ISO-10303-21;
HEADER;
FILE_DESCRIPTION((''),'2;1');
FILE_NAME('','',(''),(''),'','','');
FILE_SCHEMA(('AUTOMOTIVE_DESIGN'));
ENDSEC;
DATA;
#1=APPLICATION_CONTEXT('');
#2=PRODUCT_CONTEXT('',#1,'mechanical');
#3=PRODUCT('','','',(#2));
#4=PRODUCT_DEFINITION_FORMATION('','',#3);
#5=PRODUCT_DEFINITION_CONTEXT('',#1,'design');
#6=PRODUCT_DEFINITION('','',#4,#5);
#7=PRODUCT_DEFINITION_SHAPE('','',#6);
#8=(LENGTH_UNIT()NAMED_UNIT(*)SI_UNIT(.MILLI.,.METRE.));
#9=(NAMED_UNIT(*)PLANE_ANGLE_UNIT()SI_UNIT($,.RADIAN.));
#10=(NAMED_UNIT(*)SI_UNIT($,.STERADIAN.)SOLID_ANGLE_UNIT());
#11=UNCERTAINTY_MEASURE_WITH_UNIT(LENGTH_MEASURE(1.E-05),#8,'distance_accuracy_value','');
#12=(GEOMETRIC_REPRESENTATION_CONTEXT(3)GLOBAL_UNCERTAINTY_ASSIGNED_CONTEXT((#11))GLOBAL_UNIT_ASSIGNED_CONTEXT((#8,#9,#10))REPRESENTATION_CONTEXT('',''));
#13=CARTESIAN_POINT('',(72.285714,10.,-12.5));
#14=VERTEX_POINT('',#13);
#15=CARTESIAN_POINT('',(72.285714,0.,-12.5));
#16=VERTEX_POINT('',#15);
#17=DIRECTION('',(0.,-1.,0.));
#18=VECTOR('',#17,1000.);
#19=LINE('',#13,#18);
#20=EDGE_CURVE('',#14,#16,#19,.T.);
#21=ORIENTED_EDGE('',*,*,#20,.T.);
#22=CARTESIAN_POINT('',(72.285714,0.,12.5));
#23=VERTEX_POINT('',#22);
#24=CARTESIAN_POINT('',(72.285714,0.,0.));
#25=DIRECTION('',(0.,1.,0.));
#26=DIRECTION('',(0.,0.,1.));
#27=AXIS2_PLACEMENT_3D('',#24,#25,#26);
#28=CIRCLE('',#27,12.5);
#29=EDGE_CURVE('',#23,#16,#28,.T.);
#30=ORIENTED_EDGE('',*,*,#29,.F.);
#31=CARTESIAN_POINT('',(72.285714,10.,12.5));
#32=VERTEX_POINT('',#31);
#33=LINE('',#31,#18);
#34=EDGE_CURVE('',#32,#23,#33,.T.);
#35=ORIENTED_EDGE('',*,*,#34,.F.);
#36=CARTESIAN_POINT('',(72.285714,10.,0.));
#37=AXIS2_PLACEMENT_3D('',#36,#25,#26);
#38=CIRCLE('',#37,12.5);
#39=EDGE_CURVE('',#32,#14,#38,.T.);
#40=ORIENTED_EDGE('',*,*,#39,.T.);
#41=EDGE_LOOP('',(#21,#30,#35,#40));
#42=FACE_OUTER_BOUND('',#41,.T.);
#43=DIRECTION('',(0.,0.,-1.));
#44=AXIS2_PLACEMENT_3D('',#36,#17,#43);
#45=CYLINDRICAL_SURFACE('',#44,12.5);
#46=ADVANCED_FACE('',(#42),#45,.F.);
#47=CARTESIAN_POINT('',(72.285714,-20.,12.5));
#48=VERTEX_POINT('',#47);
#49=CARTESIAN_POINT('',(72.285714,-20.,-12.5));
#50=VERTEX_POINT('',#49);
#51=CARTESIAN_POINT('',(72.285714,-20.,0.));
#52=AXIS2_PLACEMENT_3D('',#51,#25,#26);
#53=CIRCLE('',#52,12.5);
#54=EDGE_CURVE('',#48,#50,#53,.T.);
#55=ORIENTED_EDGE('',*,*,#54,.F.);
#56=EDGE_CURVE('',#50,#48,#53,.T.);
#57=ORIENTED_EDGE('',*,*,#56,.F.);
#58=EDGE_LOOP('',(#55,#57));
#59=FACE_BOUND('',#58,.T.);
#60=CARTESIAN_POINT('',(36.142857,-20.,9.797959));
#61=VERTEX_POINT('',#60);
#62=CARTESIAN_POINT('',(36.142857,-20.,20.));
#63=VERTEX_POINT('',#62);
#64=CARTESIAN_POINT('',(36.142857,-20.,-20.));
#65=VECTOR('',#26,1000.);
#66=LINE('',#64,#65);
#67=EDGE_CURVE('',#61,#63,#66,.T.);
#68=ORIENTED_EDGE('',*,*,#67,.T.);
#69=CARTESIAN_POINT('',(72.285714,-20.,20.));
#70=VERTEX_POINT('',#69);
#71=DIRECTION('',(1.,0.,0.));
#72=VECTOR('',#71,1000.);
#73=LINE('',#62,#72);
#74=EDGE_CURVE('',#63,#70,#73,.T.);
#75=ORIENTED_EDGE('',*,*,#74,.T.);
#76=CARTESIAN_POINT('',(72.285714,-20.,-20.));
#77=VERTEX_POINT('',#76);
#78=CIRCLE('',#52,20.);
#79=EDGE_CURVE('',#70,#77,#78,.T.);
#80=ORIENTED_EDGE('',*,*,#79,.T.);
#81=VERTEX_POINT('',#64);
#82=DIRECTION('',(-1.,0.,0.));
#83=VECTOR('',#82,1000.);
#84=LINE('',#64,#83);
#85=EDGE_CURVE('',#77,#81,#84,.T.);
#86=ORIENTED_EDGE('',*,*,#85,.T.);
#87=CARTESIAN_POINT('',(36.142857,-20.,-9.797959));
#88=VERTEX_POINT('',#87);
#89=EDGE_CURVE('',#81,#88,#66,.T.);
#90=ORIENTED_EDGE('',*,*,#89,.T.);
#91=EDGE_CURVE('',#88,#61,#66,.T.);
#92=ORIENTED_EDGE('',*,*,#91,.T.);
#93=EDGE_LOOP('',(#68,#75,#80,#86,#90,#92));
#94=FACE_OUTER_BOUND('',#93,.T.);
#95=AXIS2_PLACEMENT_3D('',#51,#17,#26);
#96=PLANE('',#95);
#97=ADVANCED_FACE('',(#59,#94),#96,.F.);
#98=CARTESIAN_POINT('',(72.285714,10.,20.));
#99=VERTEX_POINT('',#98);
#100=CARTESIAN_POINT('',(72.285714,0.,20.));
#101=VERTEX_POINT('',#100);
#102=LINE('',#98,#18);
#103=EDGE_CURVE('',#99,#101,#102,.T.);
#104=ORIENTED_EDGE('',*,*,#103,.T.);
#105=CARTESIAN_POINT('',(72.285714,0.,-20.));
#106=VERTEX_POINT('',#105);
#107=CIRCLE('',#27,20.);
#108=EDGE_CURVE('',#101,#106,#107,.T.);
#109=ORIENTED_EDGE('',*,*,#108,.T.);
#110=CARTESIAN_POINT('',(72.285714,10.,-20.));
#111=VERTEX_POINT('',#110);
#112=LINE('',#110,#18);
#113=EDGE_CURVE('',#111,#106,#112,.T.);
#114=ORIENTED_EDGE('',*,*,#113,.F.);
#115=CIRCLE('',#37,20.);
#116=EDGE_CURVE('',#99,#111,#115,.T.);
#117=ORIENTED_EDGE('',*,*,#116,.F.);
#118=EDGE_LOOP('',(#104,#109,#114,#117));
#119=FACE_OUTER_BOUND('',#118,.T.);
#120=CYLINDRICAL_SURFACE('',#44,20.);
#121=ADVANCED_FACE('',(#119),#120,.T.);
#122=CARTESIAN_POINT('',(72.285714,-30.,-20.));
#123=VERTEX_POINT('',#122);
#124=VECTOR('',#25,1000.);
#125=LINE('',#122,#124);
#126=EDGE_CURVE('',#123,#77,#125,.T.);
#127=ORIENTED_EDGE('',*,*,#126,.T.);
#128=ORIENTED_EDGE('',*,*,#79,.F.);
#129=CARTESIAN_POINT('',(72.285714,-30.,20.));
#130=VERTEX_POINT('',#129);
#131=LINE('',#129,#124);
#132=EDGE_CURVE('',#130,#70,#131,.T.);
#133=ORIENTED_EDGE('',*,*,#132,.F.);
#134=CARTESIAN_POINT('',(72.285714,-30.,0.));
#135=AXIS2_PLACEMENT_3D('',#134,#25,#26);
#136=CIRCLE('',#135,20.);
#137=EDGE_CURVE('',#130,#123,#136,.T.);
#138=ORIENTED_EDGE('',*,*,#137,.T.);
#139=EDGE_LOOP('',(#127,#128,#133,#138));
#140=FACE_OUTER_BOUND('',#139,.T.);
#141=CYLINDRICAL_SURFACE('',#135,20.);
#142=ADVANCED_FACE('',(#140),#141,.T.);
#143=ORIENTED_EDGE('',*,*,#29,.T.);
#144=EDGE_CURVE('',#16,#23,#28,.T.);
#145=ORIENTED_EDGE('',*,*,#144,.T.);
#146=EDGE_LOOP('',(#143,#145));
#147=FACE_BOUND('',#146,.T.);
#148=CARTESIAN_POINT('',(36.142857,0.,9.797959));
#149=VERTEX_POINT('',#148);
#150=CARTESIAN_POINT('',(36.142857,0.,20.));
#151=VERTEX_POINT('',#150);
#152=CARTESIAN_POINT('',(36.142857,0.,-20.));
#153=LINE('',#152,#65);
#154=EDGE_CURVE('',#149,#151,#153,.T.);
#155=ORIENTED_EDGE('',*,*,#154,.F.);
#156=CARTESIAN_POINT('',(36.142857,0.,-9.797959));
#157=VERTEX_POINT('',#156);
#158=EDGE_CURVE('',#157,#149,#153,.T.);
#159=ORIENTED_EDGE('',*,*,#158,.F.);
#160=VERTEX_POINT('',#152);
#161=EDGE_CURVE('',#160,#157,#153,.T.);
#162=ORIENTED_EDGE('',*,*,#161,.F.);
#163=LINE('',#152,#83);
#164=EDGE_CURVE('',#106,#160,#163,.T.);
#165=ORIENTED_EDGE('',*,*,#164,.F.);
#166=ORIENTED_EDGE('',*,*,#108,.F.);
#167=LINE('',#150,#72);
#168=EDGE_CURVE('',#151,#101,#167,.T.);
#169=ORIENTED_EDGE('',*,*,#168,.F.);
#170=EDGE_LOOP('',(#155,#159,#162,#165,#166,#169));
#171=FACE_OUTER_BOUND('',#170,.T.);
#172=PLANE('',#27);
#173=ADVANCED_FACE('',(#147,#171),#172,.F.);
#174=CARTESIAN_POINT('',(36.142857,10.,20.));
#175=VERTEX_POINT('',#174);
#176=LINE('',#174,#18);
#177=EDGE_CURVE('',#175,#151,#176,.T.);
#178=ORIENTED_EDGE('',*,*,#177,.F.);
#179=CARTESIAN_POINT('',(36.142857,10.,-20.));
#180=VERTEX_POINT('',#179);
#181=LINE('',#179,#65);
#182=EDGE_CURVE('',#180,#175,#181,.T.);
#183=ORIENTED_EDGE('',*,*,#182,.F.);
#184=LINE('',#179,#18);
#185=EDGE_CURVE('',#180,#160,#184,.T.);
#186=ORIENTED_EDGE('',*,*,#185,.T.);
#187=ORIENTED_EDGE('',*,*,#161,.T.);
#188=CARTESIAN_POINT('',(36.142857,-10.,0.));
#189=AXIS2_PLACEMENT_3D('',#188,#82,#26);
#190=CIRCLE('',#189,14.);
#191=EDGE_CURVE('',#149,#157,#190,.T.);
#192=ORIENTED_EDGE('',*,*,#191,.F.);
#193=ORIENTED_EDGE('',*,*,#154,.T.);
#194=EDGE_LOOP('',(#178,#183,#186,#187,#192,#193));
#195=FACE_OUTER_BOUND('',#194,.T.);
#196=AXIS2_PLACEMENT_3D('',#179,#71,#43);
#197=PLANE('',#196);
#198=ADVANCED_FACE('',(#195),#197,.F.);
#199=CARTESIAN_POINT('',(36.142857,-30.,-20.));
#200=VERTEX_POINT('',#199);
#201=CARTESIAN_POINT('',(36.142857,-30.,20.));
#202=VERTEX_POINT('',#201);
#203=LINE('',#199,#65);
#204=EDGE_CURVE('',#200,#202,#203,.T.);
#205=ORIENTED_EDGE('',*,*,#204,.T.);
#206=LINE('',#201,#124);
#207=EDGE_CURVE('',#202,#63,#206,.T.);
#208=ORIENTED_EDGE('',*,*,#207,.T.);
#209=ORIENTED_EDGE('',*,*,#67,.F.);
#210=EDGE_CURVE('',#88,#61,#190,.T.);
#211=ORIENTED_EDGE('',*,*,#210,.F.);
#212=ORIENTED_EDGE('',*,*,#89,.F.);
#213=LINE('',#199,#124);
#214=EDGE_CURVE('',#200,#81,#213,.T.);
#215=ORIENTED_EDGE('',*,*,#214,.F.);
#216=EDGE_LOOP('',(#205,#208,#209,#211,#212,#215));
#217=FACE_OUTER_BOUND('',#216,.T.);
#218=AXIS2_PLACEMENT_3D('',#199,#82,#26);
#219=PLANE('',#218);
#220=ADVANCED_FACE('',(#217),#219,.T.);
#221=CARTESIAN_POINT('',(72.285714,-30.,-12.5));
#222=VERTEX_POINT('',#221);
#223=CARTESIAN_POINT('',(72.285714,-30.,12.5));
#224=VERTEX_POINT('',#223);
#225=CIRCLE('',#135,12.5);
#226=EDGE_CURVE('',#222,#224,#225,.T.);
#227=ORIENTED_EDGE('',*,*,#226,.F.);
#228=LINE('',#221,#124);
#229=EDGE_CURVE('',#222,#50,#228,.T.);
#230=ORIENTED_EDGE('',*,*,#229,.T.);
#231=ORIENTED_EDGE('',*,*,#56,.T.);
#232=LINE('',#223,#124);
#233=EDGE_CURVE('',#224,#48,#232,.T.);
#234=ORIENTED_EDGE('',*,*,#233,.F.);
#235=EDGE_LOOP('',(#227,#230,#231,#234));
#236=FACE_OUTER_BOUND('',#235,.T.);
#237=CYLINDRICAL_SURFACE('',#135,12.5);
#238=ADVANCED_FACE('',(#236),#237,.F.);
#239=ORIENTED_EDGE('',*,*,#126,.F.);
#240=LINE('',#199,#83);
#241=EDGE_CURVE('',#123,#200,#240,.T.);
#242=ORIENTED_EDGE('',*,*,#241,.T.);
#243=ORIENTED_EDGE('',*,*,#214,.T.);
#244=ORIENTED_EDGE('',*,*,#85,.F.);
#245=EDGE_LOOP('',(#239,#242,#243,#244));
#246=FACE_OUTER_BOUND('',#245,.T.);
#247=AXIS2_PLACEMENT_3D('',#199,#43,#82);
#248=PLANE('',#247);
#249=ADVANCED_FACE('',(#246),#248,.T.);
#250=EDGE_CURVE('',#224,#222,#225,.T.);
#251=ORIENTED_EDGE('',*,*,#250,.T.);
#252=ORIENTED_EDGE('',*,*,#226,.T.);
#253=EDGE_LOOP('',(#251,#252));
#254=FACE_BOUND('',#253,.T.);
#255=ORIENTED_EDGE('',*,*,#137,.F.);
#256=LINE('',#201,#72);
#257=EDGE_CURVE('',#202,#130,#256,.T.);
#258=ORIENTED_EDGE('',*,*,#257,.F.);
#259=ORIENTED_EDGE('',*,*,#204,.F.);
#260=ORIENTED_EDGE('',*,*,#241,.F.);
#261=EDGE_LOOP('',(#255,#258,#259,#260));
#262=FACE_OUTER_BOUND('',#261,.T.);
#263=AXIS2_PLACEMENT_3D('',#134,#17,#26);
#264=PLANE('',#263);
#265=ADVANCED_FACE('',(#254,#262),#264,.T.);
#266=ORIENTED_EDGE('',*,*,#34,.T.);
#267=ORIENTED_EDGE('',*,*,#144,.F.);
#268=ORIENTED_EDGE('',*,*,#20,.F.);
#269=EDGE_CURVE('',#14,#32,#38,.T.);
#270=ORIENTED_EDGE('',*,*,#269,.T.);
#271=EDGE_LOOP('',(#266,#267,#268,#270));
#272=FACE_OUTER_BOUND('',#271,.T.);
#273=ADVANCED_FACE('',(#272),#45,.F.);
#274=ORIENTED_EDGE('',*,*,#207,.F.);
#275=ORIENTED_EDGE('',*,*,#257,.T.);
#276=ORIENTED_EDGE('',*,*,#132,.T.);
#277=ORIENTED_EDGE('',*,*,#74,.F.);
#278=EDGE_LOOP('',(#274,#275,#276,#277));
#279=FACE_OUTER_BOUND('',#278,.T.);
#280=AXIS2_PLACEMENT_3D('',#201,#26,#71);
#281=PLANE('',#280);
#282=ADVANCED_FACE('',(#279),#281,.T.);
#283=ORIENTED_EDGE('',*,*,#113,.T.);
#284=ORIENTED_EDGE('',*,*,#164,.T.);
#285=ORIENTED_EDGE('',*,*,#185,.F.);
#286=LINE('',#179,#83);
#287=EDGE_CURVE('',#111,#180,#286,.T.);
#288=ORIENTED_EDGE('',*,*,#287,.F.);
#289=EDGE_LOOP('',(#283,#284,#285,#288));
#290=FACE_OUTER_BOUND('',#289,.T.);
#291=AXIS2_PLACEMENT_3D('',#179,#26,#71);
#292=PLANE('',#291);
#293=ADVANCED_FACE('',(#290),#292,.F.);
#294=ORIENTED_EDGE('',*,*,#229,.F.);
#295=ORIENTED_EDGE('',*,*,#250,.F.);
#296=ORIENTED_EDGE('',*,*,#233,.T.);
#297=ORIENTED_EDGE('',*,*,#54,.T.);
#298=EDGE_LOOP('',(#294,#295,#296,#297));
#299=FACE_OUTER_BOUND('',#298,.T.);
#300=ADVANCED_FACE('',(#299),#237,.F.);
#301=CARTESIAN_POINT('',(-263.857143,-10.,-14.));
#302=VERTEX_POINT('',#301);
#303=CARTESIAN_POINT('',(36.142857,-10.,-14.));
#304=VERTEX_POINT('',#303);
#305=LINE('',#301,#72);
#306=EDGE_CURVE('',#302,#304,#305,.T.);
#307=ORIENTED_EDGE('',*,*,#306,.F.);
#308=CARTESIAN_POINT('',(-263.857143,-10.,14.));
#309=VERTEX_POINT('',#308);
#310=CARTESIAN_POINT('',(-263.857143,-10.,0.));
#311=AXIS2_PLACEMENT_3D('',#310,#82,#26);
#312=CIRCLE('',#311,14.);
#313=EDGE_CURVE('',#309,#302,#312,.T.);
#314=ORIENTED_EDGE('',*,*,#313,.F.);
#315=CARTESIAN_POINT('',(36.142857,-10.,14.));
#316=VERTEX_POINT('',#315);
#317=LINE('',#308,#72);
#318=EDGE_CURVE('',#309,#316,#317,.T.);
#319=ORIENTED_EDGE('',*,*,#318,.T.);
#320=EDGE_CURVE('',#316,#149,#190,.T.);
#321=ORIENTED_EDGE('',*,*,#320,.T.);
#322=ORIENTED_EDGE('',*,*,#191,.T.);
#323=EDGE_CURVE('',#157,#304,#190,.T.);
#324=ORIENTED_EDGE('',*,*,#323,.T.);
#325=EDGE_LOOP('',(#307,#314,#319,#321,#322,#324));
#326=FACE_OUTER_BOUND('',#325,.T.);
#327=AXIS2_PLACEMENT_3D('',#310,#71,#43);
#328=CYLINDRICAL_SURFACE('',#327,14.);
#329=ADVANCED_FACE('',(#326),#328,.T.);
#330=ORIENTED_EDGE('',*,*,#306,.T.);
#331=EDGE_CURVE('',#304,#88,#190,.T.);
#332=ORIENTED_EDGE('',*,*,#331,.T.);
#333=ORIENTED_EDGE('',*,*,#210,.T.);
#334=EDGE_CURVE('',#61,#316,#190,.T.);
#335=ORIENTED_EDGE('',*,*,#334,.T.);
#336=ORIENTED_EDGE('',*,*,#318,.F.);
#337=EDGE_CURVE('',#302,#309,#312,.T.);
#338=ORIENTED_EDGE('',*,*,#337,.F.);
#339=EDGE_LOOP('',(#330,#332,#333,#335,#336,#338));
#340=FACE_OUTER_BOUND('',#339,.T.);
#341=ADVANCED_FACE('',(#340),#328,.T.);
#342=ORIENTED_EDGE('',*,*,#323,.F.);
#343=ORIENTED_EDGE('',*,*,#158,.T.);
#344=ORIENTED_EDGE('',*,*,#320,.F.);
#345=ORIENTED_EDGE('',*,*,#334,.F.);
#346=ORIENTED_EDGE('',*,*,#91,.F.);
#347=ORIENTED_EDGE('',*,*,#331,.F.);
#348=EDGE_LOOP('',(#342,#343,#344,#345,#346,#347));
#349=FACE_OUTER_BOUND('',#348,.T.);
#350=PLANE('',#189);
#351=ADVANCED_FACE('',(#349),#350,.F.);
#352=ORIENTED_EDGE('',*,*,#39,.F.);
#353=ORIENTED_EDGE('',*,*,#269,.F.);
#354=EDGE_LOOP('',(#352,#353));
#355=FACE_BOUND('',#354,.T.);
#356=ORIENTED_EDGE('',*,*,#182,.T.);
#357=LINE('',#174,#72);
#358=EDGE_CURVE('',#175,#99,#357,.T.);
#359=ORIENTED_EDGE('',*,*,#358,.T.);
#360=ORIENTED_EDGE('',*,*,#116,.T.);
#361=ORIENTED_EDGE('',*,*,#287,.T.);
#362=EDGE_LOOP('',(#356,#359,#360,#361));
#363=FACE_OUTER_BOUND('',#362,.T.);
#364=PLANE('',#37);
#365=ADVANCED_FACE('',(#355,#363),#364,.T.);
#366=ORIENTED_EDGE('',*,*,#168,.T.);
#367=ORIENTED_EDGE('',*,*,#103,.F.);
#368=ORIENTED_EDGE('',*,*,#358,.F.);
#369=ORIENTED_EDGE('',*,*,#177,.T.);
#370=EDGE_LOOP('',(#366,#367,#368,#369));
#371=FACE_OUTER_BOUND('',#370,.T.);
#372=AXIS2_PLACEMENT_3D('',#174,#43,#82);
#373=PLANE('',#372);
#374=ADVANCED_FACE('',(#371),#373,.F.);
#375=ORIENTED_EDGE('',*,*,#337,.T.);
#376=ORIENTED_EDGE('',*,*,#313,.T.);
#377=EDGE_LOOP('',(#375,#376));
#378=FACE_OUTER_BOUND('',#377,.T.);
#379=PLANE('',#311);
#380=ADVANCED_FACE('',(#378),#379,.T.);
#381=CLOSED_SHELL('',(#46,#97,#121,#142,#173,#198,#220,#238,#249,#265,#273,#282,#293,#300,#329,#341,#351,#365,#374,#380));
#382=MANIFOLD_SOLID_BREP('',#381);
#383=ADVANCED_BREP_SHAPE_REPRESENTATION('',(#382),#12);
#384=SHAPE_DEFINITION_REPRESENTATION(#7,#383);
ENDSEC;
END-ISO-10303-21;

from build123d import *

# Parameters (mm, degrees)
SKETCH1_R           = 12.5
BOSS_EXTRUDE1_DEPTH = 10
SKETCH2_R           = 14
BOSS_EXTRUDE2_DEPTH = 300


with BuildPart() as part:
    # Sketch1 → Boss-Extrude1 (new body)
    with BuildSketch(Plane(origin=(0, 0, 0), x_dir=(1, 0, 0), z_dir=(0, 1, 0))):
        with BuildLine():
            Line((36.142857143, 20), (72.285714286, 20))
            ThreePointArc((72.285714286, 20), (92.285714286, 0), (72.285714286, -20))
            Line((72.285714286, -20), (36.142857143, -20))
            Line((36.142857143, -20), (36.142857143, 20))
        make_face()
        with Locations(Location((72.285714286, 0, 0), (0, 0, 270))):
            Circle(SKETCH1_R, mode=Mode.SUBTRACT)
    boss_extrude1 = extrude(amount=BOSS_EXTRUDE1_DEPTH)

    # Sketch2 → Boss-Extrude2 (add)
    with BuildSketch(Plane.ZY.offset(-36.142857143)):
        with Locations(Location((0, -10, 0), (0, 0, 134.415308597))):
            Circle(SKETCH2_R)
    extrude(amount=BOSS_EXTRUDE2_DEPTH)

    # Mirror1: Boss-Extrude1 across plane
    add(boss_extrude1.mirror(Plane(origin=(0, -10, 0), x_dir=(0, 0, 1), z_dir=(0, -1, 0))))


solid = part.part
